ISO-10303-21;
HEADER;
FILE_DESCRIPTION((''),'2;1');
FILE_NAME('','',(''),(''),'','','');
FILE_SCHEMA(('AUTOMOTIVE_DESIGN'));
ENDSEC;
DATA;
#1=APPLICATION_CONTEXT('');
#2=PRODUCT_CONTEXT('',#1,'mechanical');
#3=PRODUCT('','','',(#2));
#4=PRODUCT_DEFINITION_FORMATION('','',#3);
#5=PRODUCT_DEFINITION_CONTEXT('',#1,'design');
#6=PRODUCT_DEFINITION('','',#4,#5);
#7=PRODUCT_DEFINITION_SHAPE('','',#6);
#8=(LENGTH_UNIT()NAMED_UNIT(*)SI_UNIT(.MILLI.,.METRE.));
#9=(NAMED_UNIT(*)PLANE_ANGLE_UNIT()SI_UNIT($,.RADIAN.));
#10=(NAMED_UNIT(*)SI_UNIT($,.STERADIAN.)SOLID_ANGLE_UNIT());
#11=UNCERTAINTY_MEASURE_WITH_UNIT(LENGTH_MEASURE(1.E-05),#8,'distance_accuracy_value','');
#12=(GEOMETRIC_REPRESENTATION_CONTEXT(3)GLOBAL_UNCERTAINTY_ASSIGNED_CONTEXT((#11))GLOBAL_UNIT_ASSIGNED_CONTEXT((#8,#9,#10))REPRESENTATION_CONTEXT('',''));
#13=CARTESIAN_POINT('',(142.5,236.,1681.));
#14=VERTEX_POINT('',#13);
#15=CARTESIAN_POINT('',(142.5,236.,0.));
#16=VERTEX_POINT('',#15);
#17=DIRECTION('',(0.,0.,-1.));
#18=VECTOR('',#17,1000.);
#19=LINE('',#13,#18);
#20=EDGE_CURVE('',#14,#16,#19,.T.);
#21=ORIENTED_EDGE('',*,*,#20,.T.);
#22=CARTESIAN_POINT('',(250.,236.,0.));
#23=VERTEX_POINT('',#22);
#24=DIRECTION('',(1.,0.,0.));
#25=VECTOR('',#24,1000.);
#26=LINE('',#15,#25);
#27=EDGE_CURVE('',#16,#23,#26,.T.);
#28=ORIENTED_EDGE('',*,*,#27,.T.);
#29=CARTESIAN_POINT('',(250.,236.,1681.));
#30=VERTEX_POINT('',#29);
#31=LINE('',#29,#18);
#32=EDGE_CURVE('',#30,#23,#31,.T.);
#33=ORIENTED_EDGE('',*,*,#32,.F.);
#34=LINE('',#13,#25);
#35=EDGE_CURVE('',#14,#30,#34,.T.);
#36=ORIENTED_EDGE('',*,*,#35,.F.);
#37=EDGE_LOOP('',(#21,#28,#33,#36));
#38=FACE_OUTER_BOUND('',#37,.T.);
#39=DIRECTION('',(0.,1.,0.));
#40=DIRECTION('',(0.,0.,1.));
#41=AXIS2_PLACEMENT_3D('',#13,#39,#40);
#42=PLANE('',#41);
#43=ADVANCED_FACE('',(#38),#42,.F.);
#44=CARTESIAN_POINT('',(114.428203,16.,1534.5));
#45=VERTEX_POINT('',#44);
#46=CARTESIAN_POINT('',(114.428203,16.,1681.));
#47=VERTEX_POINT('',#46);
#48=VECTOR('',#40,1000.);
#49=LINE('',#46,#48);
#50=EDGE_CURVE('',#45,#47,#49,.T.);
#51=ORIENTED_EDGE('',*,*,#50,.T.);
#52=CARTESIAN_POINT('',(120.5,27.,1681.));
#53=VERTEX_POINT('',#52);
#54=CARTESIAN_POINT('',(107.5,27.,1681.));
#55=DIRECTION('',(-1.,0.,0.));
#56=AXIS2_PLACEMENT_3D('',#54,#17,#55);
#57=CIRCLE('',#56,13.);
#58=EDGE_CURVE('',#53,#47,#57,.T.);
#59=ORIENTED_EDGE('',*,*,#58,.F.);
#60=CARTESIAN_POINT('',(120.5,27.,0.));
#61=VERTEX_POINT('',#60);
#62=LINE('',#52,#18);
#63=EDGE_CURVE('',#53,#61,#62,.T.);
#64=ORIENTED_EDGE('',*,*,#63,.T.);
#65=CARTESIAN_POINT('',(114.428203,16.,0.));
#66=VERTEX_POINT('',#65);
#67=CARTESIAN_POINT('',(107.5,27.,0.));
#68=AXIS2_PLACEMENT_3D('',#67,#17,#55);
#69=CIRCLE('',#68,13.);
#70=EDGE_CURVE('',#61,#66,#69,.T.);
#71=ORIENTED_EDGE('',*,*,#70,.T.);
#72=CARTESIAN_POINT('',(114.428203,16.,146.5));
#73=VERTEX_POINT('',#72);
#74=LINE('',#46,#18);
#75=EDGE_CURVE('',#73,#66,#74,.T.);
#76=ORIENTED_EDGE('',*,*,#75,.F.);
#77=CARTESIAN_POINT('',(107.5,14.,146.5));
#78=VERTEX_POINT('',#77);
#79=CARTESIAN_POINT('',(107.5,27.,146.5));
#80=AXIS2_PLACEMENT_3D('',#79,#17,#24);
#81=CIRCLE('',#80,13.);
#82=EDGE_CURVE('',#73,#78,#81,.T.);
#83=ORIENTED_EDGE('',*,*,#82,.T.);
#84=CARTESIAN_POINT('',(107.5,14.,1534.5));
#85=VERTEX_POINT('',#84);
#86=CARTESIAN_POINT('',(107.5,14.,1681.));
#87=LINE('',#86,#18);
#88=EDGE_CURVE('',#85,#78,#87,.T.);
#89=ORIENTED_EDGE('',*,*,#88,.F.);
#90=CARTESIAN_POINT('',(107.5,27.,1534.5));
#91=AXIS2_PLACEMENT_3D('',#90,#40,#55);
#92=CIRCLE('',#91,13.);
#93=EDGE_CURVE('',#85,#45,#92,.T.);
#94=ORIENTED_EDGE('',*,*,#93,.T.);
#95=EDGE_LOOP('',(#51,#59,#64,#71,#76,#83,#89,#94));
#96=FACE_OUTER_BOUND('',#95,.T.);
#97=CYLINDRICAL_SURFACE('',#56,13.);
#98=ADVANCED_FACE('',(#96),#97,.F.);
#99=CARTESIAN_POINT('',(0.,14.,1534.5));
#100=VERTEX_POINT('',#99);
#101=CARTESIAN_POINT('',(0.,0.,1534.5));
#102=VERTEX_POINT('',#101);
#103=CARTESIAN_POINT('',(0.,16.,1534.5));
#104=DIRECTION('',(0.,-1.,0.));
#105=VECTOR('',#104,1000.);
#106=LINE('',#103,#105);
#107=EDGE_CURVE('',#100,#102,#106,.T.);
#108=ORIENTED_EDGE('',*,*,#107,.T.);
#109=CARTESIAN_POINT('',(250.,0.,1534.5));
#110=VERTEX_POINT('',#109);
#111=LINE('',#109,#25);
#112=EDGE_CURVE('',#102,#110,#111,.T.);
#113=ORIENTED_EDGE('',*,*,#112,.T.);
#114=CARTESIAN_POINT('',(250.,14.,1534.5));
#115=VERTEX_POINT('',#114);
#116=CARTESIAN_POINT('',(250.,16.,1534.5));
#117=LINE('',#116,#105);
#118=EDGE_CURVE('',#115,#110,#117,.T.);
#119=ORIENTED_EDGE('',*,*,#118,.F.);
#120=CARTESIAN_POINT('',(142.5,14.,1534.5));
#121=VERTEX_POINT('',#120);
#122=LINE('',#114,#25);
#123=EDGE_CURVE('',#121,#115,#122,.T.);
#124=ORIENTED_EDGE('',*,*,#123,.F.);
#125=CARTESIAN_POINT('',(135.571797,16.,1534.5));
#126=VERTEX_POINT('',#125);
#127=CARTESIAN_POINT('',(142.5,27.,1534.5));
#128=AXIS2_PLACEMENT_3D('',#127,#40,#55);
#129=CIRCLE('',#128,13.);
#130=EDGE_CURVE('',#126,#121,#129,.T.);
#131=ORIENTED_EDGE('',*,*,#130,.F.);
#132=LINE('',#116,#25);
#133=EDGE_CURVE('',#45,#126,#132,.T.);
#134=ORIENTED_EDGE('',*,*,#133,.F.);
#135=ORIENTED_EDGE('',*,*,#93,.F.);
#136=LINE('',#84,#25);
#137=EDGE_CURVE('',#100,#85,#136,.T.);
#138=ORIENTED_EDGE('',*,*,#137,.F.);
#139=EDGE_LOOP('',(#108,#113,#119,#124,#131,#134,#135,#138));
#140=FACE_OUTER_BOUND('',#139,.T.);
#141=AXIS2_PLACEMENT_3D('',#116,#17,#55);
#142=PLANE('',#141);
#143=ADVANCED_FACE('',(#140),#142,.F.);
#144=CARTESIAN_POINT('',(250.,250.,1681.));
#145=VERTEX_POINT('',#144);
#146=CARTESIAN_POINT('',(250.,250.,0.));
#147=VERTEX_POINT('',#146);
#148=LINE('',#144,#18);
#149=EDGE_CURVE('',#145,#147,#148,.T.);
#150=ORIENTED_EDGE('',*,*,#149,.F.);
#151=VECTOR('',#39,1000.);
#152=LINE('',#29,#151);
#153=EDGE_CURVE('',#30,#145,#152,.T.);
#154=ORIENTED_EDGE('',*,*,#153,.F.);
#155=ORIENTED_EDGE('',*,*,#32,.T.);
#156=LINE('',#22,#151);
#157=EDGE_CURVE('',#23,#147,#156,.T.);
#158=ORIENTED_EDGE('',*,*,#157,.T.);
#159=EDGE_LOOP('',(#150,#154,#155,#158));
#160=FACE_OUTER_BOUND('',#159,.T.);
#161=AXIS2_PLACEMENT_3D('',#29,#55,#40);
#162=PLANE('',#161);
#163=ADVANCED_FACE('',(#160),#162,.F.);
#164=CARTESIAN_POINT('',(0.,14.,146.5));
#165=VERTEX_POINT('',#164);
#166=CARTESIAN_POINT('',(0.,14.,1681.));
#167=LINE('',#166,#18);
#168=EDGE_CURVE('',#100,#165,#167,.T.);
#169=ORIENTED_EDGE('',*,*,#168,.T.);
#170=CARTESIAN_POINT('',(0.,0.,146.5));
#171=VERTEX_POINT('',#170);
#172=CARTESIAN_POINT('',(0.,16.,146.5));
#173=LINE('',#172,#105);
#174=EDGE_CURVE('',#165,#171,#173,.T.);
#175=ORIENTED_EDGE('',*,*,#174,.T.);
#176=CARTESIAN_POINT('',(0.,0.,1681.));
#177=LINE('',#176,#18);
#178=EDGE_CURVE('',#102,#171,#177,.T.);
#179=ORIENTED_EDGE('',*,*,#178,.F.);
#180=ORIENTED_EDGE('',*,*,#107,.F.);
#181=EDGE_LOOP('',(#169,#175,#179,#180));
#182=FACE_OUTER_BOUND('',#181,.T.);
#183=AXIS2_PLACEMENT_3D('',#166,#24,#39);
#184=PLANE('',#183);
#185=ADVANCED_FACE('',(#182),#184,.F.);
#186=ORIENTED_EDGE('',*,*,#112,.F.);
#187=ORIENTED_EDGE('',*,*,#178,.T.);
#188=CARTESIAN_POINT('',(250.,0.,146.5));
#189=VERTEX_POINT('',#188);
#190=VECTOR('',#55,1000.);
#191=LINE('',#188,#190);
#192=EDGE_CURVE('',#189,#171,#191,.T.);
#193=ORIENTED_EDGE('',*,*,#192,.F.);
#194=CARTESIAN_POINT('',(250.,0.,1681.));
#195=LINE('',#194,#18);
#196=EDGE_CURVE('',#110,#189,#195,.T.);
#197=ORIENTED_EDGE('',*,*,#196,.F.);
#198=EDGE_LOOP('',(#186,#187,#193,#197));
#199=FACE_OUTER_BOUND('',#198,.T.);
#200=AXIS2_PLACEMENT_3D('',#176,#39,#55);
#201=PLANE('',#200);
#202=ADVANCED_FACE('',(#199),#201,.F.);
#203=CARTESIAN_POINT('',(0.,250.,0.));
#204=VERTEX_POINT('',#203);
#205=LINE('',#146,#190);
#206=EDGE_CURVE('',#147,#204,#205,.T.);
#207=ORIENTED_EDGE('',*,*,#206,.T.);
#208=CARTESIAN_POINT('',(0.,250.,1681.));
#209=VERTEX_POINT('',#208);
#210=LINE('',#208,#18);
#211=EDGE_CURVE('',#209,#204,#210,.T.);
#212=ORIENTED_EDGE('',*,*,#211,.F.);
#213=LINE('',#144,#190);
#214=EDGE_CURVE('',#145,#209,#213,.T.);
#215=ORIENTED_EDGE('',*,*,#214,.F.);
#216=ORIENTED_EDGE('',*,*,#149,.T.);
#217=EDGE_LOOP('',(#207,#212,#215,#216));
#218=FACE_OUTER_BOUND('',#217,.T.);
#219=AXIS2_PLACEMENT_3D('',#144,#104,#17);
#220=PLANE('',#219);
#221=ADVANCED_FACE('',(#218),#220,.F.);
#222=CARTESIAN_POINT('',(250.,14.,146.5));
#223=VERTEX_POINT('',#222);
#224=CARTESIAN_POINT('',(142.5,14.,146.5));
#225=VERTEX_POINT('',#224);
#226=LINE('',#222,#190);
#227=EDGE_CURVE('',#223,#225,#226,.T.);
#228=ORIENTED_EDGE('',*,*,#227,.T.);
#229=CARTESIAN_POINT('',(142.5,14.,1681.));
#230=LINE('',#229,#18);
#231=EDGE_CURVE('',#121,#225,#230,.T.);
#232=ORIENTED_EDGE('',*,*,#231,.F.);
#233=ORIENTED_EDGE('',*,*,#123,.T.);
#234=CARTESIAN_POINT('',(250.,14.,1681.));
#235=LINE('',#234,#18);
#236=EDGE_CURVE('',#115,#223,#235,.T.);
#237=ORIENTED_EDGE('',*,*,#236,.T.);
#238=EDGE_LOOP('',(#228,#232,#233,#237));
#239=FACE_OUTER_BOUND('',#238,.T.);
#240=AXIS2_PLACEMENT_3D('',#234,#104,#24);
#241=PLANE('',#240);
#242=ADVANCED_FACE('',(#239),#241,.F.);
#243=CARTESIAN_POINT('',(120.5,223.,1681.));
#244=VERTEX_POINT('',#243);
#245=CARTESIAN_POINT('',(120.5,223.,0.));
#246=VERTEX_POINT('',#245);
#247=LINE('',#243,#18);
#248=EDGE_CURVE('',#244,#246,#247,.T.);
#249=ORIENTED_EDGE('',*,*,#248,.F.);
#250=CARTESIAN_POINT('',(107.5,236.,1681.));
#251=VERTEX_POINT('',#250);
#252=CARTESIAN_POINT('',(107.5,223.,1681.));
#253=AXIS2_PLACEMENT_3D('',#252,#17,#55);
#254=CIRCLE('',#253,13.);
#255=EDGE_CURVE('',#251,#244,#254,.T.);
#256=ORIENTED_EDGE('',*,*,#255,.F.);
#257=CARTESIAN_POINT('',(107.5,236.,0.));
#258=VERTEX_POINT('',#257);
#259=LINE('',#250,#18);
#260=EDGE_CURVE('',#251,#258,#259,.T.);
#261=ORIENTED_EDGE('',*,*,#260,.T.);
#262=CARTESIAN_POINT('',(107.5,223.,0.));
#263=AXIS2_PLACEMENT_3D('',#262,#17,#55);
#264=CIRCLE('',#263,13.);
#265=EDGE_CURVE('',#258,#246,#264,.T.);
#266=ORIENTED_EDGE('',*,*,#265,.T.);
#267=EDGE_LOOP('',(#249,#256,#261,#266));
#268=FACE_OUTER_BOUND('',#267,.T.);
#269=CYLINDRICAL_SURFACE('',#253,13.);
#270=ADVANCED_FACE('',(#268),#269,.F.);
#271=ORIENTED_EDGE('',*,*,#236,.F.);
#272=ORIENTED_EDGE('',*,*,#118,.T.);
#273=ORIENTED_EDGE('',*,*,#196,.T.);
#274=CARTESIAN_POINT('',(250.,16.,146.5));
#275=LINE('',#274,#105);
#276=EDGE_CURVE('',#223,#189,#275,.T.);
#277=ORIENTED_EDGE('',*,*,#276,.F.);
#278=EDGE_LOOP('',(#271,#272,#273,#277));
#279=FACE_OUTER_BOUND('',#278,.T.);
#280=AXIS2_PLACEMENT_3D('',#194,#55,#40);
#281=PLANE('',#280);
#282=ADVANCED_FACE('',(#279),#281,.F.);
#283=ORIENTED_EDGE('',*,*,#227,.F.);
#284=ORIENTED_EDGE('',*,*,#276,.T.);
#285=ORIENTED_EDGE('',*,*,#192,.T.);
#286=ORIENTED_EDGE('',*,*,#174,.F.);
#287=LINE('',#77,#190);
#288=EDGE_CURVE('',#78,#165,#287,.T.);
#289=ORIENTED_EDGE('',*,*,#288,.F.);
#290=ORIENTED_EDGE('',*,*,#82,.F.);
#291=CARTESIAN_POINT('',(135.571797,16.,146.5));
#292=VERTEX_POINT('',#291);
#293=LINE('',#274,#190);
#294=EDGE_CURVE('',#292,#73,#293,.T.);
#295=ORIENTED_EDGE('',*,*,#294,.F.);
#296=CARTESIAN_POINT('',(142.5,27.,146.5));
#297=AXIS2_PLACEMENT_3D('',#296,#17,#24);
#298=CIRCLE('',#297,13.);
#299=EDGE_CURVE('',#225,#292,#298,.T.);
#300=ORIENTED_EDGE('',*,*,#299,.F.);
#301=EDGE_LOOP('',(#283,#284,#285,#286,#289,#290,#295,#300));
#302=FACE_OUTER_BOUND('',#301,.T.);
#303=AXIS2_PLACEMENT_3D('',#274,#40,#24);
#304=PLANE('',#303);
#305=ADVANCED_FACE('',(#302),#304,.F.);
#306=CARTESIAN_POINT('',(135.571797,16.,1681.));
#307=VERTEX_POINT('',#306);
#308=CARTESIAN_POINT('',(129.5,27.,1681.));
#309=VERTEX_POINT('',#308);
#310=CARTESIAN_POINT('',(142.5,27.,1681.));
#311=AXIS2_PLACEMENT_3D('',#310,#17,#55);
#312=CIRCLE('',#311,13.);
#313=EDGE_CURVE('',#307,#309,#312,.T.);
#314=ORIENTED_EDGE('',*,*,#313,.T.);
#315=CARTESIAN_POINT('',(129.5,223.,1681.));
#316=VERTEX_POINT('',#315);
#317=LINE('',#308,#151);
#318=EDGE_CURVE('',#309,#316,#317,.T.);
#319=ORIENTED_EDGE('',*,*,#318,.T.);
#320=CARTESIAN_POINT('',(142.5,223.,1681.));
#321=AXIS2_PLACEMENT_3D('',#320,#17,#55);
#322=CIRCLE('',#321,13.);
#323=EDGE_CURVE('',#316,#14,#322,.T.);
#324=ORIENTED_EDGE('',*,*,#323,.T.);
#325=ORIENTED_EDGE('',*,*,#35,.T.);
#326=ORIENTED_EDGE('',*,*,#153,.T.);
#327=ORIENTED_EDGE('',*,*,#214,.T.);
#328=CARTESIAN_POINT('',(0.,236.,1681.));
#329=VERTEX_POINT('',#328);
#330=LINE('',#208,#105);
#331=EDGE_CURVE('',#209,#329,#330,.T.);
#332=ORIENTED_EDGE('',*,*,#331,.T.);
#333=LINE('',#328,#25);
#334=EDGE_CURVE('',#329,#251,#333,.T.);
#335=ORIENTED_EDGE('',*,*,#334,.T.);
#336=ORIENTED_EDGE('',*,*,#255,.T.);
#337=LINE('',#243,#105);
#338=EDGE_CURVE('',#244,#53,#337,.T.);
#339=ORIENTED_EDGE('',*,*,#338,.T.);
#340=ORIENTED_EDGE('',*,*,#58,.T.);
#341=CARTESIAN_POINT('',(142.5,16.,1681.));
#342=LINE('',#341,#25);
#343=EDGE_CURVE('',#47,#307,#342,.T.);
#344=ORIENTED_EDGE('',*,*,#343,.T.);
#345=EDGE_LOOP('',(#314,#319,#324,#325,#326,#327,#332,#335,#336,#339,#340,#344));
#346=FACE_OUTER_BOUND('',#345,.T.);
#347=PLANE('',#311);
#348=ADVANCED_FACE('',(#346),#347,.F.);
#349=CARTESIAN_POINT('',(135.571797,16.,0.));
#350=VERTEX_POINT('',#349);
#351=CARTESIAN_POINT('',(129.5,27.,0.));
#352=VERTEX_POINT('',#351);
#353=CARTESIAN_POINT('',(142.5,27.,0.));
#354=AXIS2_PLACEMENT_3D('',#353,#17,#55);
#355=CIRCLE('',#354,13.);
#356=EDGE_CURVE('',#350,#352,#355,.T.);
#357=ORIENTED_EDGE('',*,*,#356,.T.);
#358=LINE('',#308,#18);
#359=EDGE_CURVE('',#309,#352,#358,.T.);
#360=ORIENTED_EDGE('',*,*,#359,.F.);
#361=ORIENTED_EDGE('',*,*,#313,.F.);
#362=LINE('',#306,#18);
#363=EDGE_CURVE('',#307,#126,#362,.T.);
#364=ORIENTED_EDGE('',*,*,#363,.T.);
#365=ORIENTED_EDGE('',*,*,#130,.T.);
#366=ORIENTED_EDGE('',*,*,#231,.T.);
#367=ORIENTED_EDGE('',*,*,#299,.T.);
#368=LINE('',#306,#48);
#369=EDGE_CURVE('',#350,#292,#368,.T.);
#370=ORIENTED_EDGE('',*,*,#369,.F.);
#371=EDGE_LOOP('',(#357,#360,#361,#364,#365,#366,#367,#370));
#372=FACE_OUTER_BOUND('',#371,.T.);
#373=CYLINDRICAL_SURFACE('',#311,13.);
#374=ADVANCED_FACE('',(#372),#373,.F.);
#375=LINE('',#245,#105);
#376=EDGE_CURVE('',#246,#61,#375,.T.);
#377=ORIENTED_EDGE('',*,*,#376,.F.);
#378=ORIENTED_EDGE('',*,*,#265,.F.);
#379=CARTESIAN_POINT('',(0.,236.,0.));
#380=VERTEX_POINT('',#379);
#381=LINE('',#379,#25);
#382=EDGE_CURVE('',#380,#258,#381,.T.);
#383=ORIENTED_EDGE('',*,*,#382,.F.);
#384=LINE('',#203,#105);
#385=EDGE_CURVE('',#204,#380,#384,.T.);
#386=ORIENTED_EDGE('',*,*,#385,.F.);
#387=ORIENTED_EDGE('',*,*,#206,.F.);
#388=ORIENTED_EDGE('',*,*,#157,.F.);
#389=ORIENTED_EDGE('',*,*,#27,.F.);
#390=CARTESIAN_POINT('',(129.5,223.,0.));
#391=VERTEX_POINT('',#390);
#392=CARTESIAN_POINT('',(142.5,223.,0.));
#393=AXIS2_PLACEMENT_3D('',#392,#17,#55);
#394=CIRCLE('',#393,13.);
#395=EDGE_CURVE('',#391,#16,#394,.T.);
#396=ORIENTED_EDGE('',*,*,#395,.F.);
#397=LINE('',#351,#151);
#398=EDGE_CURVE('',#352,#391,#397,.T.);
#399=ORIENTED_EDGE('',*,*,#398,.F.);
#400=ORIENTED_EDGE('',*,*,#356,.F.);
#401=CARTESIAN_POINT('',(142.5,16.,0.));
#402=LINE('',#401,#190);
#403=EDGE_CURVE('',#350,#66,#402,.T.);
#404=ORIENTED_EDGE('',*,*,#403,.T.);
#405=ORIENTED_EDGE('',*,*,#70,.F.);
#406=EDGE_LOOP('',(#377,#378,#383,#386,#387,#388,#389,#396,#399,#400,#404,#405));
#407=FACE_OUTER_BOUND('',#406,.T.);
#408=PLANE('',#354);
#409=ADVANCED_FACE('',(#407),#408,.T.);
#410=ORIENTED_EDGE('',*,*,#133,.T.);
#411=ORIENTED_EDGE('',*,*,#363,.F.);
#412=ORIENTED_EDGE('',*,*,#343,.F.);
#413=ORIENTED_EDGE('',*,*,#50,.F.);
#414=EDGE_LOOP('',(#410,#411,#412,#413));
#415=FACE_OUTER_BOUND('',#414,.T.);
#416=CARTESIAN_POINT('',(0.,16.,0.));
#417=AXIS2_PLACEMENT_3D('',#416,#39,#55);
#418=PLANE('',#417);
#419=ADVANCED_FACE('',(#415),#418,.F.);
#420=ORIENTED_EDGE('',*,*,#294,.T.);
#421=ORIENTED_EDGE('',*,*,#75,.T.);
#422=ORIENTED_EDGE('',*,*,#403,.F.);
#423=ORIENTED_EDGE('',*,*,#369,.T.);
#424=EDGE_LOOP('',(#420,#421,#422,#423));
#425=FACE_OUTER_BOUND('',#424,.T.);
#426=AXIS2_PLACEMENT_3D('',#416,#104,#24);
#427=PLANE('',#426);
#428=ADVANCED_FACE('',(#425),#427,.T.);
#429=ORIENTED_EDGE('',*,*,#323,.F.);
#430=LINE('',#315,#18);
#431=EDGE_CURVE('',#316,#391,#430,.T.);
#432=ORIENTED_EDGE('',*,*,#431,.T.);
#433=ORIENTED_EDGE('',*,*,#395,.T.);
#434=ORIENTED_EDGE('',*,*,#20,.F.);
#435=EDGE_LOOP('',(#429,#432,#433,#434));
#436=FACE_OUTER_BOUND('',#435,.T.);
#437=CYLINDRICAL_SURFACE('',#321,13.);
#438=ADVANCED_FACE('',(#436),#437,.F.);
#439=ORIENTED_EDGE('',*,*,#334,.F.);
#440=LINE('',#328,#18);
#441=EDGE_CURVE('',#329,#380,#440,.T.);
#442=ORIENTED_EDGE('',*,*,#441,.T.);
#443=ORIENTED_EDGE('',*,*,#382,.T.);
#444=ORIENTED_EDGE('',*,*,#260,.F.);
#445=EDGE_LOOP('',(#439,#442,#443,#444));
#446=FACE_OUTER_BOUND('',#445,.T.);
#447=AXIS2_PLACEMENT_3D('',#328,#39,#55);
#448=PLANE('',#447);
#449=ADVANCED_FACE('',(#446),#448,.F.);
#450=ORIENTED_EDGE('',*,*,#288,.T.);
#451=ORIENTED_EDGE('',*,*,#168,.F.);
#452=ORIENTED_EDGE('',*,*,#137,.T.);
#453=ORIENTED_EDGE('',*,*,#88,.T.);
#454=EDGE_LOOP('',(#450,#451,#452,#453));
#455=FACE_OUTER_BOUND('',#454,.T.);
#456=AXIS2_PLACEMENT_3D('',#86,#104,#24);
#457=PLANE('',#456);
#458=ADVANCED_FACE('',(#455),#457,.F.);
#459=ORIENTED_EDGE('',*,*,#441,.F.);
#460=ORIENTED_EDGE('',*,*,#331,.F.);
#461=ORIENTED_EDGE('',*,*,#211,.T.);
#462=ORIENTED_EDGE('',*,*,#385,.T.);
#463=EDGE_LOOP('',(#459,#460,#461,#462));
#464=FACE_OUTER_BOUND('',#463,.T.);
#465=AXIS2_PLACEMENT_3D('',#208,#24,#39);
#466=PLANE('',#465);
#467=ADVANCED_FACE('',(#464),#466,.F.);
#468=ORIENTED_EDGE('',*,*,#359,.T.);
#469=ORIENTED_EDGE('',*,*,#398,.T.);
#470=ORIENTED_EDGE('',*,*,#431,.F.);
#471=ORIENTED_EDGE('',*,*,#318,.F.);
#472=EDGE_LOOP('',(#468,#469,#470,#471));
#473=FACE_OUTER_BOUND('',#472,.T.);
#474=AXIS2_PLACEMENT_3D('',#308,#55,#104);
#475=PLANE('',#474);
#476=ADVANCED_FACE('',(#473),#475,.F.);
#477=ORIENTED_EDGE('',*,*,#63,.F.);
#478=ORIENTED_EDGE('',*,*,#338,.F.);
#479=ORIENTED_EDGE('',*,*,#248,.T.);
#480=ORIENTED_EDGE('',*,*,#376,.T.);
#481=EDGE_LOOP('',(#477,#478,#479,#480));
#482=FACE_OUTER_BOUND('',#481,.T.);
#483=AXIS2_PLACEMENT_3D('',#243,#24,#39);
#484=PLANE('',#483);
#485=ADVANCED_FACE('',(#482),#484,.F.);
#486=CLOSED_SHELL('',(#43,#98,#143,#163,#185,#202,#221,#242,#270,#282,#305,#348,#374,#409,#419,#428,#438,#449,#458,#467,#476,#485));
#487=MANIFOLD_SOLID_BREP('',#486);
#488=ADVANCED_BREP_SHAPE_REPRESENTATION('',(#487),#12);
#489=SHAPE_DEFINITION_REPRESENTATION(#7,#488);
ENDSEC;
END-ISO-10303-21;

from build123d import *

# Parameters (mm, degrees)
BOSS_EXTRUDE1_DEPTH = 1681
SKETCH3_W           = 250
SKETCH3_H           = 146.5
CUT_EXTRUDE1_DEPTH  = 16


with BuildPart() as part:
    # Sketch1 → Boss-Extrude1 (new body)
    with BuildSketch(Plane.XY):
        with BuildLine():
            Line((0, 0), (250, 0))
            Line((250, 0), (250, 14))
            Line((250, 14), (142.5, 14))
            ThreePointArc((142.5, 14), (133.307611845, 17.807611845), (129.5, 27))
            Line((129.5, 27), (129.5, 223))
            ThreePointArc((129.5, 223), (133.307611845, 232.192388155), (142.5, 236))
            Line((142.5, 236), (250, 236))
            Line((250, 236), (250, 250))
            Line((250, 250), (0, 250))
            Line((0, 250), (0, 236))
            Line((0, 236), (107.5, 236))
            ThreePointArc((107.5, 236), (116.692388155, 232.192388155), (120.5, 223))
            Line((120.5, 223), (120.5, 27))
            ThreePointArc((120.5, 27), (116.692388155, 17.807611845), (107.5, 14))
            Line((107.5, 14), (0, 14))
            Line((0, 14), (0, 0))
        make_face()
    extrude(amount=BOSS_EXTRUDE1_DEPTH)

    # Sketch3 → Cut-Extrude1 (cut)
    with BuildSketch(Plane(origin=(0, 0, 0), x_dir=(-1, 0, 0), z_dir=(0, -1, 0))):
        with Locations((-125, -73.25)):
            Rectangle(SKETCH3_W, SKETCH3_H)
        with Locations((-125, -1607.75)):
            Rectangle(SKETCH3_W, SKETCH3_H)
    extrude(amount=-CUT_EXTRUDE1_DEPTH, mode=Mode.SUBTRACT)


solid = part.part
